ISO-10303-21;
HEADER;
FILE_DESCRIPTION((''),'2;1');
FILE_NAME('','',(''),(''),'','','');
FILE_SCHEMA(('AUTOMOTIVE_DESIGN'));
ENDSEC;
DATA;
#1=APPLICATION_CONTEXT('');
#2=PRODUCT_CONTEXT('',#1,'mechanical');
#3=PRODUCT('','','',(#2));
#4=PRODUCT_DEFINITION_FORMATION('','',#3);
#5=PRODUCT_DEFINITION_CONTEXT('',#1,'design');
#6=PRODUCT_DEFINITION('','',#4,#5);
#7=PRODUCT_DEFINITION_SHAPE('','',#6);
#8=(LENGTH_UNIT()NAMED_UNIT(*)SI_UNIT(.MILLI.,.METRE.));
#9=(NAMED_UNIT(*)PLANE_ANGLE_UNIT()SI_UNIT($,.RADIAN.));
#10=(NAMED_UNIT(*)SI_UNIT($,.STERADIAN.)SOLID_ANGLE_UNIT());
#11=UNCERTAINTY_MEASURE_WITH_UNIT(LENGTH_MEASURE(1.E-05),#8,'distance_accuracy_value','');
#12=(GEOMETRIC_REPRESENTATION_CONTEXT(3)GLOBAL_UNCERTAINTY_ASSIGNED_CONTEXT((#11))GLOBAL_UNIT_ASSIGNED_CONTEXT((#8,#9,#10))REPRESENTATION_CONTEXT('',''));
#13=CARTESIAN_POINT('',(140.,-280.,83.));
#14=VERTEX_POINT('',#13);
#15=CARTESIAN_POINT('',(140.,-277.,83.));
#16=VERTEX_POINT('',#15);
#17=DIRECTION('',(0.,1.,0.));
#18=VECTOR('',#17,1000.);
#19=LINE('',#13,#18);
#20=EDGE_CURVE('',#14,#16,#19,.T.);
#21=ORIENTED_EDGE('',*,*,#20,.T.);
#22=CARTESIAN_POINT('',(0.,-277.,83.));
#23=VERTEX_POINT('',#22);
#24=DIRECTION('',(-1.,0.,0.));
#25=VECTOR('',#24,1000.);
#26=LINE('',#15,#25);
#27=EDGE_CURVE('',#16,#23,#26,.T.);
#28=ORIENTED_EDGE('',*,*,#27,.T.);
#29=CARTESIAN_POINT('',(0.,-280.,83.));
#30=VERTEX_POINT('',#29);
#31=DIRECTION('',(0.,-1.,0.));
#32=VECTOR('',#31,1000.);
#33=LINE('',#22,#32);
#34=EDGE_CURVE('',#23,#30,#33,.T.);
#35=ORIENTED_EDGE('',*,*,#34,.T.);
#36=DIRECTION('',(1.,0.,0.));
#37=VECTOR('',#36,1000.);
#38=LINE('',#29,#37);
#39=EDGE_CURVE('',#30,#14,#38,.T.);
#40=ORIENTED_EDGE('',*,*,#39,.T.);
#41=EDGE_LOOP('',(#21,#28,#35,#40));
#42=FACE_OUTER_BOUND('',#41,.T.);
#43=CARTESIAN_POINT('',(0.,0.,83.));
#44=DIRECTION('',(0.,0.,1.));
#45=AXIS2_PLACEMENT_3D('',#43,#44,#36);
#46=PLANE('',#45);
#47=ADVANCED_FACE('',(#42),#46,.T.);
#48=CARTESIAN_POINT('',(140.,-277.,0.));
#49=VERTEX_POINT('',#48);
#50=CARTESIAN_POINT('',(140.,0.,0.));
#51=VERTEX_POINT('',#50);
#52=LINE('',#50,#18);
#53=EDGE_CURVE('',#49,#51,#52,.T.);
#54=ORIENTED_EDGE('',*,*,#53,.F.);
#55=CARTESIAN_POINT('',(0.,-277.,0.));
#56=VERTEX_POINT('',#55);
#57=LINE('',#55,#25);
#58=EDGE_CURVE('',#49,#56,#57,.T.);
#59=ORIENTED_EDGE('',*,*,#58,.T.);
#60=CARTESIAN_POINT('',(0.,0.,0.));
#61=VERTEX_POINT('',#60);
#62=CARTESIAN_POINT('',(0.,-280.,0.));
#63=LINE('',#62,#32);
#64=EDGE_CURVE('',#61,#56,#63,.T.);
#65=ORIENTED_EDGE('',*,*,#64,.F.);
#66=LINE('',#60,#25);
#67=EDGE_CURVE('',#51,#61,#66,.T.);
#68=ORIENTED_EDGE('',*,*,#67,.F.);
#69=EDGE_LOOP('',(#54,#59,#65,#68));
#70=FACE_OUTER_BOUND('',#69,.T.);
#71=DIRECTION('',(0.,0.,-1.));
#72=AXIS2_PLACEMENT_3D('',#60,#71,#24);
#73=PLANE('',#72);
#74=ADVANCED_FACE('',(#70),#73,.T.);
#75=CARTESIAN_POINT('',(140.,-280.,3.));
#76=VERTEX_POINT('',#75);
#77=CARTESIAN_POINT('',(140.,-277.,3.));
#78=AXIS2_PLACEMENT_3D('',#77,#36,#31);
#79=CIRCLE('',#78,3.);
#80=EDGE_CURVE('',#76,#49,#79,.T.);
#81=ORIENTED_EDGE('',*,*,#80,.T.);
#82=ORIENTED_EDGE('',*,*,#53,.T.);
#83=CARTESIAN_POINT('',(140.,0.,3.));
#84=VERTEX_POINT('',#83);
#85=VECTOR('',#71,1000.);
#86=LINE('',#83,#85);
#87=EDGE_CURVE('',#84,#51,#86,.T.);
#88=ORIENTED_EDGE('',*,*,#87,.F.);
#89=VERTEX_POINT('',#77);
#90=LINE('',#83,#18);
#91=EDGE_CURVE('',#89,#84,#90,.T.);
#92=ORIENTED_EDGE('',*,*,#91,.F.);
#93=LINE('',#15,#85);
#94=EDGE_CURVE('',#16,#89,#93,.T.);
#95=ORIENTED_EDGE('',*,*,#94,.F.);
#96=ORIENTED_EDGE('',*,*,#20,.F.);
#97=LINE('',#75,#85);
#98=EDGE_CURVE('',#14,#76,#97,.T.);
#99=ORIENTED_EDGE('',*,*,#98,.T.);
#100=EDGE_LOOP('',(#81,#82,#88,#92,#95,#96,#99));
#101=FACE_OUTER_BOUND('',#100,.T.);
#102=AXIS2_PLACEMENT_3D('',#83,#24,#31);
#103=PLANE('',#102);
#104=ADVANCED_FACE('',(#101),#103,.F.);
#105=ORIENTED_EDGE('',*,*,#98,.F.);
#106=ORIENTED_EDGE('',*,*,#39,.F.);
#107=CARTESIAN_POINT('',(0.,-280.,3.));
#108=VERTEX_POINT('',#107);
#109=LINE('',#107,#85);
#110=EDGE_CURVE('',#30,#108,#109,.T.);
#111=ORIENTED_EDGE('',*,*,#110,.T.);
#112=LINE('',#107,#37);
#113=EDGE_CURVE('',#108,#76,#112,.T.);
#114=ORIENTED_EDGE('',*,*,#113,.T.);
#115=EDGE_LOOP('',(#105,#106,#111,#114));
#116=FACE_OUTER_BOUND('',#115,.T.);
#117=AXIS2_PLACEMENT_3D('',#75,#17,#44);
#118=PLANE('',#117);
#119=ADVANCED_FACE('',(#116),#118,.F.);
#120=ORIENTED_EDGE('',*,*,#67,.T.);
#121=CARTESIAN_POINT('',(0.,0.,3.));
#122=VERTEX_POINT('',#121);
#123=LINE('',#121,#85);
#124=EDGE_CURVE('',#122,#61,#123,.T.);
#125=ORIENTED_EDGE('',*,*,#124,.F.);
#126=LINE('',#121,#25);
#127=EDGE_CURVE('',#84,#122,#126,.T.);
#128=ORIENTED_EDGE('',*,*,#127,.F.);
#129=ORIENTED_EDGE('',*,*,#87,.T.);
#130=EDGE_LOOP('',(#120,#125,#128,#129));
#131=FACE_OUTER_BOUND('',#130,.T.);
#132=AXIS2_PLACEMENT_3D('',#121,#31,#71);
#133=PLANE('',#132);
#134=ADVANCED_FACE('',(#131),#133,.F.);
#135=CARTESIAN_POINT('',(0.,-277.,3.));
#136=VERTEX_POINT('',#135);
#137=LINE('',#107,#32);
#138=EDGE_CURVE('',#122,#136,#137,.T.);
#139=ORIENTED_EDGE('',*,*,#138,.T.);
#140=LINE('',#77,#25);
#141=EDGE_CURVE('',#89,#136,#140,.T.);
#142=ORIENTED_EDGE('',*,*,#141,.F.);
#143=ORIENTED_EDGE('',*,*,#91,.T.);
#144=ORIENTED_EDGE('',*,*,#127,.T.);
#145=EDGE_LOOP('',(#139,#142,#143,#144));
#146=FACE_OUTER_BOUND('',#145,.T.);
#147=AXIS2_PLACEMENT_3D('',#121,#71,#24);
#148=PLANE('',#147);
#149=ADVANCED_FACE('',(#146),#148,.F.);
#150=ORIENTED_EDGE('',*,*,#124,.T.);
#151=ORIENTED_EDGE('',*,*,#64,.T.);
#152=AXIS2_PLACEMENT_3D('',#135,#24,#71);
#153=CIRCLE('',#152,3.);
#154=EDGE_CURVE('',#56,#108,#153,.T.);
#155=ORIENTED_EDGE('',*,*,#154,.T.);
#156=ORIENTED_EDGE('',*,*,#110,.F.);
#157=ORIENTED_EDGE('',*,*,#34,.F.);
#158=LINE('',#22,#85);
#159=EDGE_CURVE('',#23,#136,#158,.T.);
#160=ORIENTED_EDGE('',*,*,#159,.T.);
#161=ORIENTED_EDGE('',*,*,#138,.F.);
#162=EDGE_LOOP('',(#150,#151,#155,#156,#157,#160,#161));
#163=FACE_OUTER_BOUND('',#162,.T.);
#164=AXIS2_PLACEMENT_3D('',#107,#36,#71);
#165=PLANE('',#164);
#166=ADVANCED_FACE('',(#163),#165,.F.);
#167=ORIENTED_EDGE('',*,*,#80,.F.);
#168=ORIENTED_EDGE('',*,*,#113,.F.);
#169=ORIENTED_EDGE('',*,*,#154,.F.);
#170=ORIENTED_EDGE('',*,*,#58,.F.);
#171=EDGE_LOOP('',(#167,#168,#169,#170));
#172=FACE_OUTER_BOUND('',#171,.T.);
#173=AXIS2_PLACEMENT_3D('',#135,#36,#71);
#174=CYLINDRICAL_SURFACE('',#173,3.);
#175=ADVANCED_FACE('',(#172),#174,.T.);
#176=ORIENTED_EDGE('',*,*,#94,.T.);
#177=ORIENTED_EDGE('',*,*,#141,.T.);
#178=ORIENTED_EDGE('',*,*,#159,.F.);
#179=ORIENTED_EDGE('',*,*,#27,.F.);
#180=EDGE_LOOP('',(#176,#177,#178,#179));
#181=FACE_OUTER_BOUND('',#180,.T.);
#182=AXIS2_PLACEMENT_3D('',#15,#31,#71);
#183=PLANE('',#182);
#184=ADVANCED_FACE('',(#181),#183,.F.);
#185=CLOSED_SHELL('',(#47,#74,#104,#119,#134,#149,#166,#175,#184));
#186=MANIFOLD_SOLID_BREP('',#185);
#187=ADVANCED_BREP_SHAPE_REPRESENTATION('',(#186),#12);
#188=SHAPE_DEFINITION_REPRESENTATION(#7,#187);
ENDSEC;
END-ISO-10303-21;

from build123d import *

# Parameters (mm, degrees)
SKETCH_1_W      = 140
SKETCH_1_H      = 280
EXTRUDE_1_DEPTH = 3
SKETCH_2_W      = 140
SKETCH_2_H      = 3
EXTRUDE_2_DEPTH = 80
FILLET_1_R      = 3


with BuildPart() as part:
    # 草图1 → 凸台-拉伸1 (new body)
    with BuildSketch(Plane.XY):
        with Locations((70, -140)):
            Rectangle(SKETCH_1_W, SKETCH_1_H)
    extrude(amount=EXTRUDE_1_DEPTH)

    # 草图2 → 凸台-拉伸2 (add)
    with BuildSketch(Plane.XY.offset(3)):
        with Locations((70, -278.5)):
            Rectangle(SKETCH_2_W, SKETCH_2_H)
    extrude(amount=EXTRUDE_2_DEPTH)

    # 圆角1
    fillet_1_edges = [part.edges().sort_by_distance(p)[0] for p in [
        (70, -280, 0),
    ]]
    fillet(fillet_1_edges, radius=FILLET_1_R)


solid = part.part
